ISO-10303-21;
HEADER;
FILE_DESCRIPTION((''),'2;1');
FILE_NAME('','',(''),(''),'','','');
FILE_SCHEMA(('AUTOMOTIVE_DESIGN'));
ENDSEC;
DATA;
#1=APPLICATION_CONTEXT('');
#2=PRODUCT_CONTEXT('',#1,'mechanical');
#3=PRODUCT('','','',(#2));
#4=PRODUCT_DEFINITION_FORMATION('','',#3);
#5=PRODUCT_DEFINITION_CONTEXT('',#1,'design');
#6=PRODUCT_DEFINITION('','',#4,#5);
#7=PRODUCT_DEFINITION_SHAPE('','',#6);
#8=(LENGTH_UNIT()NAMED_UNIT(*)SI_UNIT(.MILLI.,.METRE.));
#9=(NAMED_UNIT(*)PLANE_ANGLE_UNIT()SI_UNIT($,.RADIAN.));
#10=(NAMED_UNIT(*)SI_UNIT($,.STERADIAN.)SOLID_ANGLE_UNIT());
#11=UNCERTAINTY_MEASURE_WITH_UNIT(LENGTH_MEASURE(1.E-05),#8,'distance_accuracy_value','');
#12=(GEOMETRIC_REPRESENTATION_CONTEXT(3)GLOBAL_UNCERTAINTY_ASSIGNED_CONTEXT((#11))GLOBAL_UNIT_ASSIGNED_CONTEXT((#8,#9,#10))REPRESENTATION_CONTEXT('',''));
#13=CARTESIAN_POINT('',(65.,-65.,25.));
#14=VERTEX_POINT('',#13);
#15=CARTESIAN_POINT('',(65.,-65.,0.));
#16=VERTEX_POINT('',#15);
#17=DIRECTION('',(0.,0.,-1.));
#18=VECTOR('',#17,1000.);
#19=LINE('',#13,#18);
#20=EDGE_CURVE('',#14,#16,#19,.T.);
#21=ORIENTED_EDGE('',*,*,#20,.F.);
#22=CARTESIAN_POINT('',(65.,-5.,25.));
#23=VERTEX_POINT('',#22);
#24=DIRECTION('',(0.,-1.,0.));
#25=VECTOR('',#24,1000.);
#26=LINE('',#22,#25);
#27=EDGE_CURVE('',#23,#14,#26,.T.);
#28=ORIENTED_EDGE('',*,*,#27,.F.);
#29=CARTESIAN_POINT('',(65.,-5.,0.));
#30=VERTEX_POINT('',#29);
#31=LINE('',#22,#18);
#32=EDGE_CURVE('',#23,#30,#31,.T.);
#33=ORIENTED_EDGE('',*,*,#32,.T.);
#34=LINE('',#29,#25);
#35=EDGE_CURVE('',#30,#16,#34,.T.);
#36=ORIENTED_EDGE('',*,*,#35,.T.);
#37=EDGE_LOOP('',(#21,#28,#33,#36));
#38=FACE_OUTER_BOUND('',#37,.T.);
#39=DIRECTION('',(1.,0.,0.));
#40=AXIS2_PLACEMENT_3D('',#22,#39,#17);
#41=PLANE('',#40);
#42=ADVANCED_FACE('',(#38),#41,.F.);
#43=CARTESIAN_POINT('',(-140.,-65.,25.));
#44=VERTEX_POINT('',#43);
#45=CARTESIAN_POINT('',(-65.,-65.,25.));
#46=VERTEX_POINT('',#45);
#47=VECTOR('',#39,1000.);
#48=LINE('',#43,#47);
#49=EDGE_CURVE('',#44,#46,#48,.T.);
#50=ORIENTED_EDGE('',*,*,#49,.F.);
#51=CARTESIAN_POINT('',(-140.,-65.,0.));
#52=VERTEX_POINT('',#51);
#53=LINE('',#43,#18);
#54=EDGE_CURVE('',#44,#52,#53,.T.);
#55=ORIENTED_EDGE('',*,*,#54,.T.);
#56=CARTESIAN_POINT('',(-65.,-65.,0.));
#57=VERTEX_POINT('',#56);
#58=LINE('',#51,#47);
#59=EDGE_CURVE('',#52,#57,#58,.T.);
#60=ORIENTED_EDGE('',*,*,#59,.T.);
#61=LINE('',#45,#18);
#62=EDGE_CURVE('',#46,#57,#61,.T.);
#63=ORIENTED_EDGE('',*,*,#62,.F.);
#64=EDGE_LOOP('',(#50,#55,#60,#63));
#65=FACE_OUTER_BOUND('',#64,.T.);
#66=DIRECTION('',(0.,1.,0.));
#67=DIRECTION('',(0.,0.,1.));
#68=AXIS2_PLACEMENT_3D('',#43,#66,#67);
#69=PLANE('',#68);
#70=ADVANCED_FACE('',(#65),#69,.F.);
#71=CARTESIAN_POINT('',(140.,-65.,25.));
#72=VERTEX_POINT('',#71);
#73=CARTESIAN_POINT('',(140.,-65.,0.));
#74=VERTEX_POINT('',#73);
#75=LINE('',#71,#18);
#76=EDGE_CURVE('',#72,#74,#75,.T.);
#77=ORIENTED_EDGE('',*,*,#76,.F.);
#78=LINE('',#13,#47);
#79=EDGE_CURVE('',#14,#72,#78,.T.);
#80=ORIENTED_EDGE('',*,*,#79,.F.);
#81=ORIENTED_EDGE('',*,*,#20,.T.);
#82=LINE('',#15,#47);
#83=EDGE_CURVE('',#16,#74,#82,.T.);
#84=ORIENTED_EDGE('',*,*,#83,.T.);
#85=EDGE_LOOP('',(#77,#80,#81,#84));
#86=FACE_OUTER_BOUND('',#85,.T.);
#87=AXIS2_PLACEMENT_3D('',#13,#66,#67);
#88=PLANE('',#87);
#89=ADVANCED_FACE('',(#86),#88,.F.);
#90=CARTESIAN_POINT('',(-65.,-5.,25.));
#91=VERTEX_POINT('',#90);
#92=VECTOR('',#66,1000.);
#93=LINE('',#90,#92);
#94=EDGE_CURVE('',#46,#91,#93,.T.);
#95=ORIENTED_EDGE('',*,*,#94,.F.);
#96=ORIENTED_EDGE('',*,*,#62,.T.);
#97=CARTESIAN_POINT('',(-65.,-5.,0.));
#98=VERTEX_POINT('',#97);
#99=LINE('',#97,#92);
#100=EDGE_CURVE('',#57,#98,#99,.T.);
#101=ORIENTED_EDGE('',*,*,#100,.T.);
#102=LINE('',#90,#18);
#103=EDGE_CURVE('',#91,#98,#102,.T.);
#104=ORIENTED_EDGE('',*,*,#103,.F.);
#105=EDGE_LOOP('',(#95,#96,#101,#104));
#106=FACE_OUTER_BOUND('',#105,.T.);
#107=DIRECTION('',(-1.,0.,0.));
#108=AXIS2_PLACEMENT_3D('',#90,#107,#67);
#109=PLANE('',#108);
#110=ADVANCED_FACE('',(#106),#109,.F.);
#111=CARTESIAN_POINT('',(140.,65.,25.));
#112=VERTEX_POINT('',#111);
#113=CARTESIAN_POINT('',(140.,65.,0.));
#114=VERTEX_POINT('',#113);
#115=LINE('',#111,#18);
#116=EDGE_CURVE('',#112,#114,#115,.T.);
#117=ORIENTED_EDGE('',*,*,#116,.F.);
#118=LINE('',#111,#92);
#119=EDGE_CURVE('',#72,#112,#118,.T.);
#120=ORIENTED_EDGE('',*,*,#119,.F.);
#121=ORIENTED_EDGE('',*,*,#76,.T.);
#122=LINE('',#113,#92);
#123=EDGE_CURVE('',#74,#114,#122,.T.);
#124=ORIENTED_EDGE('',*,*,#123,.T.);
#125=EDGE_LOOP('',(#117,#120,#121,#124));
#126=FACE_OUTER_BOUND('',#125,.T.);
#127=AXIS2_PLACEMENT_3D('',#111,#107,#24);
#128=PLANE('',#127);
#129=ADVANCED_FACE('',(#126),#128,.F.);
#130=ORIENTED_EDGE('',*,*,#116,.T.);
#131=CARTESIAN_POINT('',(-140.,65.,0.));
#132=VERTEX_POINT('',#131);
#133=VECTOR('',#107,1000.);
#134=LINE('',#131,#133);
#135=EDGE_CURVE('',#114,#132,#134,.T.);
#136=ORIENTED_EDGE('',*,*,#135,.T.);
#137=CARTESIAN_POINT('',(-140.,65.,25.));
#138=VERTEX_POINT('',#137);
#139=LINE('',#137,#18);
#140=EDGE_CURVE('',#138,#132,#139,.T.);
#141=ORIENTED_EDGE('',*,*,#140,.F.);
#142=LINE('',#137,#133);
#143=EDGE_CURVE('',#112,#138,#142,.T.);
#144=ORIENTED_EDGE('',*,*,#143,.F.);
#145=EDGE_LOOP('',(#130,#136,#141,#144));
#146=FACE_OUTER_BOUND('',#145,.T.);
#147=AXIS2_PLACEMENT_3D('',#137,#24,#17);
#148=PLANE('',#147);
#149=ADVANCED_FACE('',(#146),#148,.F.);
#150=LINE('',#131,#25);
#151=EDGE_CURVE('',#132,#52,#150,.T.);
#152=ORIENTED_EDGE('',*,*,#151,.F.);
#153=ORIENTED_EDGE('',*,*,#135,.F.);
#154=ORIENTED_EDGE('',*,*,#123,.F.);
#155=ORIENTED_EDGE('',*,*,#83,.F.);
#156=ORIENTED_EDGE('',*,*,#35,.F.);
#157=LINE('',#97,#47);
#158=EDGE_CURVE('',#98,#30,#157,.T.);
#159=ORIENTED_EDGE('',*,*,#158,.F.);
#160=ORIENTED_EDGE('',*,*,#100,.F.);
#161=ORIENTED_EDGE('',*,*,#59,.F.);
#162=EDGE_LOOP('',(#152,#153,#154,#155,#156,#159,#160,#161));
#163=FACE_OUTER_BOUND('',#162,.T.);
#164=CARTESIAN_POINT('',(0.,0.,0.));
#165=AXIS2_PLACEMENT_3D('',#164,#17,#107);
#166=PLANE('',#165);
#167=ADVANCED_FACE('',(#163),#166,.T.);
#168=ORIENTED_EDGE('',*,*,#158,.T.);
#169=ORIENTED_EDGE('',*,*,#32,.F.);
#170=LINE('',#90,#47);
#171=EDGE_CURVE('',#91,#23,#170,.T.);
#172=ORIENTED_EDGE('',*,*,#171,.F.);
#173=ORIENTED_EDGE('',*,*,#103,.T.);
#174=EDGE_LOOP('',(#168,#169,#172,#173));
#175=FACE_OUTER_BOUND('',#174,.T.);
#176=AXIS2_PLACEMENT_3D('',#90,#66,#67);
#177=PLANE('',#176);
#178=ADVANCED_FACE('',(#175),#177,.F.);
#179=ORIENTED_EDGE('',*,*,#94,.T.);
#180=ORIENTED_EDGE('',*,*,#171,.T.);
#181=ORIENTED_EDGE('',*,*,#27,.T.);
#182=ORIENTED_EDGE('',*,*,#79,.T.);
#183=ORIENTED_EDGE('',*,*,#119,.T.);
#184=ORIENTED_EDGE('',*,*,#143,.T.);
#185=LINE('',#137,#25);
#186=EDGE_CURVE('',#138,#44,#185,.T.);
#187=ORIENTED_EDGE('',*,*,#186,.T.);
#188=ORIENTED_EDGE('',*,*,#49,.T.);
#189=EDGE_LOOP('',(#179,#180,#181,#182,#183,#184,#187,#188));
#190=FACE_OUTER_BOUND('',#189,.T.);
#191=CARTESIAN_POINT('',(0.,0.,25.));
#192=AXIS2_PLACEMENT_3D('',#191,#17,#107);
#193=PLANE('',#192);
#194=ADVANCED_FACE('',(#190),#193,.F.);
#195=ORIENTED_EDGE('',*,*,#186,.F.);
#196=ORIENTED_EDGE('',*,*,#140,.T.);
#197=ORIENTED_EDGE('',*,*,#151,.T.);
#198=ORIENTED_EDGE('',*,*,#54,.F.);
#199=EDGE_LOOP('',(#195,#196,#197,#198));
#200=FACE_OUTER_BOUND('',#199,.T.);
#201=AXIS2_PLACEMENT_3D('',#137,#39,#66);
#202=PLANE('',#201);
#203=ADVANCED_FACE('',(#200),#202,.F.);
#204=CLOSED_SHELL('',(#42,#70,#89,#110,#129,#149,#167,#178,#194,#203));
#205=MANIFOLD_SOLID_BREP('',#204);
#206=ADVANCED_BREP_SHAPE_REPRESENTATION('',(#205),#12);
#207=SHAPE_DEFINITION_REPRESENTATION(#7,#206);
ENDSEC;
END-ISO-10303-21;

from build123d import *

# Parameters (mm, degrees)
BOSS_EXTRUDE1_DEPTH = 25


with BuildPart() as part:
    # Sketch1 → Boss-Extrude1 (new body)
    with BuildSketch(Plane.XY):
        Polygon((-140, 65), (140, 65), (140, -65), (65, -65), (65, -5), (-65, -5), (-65, -65), (-140, -65), align=None)
    extrude(amount=BOSS_EXTRUDE1_DEPTH)


solid = part.part
